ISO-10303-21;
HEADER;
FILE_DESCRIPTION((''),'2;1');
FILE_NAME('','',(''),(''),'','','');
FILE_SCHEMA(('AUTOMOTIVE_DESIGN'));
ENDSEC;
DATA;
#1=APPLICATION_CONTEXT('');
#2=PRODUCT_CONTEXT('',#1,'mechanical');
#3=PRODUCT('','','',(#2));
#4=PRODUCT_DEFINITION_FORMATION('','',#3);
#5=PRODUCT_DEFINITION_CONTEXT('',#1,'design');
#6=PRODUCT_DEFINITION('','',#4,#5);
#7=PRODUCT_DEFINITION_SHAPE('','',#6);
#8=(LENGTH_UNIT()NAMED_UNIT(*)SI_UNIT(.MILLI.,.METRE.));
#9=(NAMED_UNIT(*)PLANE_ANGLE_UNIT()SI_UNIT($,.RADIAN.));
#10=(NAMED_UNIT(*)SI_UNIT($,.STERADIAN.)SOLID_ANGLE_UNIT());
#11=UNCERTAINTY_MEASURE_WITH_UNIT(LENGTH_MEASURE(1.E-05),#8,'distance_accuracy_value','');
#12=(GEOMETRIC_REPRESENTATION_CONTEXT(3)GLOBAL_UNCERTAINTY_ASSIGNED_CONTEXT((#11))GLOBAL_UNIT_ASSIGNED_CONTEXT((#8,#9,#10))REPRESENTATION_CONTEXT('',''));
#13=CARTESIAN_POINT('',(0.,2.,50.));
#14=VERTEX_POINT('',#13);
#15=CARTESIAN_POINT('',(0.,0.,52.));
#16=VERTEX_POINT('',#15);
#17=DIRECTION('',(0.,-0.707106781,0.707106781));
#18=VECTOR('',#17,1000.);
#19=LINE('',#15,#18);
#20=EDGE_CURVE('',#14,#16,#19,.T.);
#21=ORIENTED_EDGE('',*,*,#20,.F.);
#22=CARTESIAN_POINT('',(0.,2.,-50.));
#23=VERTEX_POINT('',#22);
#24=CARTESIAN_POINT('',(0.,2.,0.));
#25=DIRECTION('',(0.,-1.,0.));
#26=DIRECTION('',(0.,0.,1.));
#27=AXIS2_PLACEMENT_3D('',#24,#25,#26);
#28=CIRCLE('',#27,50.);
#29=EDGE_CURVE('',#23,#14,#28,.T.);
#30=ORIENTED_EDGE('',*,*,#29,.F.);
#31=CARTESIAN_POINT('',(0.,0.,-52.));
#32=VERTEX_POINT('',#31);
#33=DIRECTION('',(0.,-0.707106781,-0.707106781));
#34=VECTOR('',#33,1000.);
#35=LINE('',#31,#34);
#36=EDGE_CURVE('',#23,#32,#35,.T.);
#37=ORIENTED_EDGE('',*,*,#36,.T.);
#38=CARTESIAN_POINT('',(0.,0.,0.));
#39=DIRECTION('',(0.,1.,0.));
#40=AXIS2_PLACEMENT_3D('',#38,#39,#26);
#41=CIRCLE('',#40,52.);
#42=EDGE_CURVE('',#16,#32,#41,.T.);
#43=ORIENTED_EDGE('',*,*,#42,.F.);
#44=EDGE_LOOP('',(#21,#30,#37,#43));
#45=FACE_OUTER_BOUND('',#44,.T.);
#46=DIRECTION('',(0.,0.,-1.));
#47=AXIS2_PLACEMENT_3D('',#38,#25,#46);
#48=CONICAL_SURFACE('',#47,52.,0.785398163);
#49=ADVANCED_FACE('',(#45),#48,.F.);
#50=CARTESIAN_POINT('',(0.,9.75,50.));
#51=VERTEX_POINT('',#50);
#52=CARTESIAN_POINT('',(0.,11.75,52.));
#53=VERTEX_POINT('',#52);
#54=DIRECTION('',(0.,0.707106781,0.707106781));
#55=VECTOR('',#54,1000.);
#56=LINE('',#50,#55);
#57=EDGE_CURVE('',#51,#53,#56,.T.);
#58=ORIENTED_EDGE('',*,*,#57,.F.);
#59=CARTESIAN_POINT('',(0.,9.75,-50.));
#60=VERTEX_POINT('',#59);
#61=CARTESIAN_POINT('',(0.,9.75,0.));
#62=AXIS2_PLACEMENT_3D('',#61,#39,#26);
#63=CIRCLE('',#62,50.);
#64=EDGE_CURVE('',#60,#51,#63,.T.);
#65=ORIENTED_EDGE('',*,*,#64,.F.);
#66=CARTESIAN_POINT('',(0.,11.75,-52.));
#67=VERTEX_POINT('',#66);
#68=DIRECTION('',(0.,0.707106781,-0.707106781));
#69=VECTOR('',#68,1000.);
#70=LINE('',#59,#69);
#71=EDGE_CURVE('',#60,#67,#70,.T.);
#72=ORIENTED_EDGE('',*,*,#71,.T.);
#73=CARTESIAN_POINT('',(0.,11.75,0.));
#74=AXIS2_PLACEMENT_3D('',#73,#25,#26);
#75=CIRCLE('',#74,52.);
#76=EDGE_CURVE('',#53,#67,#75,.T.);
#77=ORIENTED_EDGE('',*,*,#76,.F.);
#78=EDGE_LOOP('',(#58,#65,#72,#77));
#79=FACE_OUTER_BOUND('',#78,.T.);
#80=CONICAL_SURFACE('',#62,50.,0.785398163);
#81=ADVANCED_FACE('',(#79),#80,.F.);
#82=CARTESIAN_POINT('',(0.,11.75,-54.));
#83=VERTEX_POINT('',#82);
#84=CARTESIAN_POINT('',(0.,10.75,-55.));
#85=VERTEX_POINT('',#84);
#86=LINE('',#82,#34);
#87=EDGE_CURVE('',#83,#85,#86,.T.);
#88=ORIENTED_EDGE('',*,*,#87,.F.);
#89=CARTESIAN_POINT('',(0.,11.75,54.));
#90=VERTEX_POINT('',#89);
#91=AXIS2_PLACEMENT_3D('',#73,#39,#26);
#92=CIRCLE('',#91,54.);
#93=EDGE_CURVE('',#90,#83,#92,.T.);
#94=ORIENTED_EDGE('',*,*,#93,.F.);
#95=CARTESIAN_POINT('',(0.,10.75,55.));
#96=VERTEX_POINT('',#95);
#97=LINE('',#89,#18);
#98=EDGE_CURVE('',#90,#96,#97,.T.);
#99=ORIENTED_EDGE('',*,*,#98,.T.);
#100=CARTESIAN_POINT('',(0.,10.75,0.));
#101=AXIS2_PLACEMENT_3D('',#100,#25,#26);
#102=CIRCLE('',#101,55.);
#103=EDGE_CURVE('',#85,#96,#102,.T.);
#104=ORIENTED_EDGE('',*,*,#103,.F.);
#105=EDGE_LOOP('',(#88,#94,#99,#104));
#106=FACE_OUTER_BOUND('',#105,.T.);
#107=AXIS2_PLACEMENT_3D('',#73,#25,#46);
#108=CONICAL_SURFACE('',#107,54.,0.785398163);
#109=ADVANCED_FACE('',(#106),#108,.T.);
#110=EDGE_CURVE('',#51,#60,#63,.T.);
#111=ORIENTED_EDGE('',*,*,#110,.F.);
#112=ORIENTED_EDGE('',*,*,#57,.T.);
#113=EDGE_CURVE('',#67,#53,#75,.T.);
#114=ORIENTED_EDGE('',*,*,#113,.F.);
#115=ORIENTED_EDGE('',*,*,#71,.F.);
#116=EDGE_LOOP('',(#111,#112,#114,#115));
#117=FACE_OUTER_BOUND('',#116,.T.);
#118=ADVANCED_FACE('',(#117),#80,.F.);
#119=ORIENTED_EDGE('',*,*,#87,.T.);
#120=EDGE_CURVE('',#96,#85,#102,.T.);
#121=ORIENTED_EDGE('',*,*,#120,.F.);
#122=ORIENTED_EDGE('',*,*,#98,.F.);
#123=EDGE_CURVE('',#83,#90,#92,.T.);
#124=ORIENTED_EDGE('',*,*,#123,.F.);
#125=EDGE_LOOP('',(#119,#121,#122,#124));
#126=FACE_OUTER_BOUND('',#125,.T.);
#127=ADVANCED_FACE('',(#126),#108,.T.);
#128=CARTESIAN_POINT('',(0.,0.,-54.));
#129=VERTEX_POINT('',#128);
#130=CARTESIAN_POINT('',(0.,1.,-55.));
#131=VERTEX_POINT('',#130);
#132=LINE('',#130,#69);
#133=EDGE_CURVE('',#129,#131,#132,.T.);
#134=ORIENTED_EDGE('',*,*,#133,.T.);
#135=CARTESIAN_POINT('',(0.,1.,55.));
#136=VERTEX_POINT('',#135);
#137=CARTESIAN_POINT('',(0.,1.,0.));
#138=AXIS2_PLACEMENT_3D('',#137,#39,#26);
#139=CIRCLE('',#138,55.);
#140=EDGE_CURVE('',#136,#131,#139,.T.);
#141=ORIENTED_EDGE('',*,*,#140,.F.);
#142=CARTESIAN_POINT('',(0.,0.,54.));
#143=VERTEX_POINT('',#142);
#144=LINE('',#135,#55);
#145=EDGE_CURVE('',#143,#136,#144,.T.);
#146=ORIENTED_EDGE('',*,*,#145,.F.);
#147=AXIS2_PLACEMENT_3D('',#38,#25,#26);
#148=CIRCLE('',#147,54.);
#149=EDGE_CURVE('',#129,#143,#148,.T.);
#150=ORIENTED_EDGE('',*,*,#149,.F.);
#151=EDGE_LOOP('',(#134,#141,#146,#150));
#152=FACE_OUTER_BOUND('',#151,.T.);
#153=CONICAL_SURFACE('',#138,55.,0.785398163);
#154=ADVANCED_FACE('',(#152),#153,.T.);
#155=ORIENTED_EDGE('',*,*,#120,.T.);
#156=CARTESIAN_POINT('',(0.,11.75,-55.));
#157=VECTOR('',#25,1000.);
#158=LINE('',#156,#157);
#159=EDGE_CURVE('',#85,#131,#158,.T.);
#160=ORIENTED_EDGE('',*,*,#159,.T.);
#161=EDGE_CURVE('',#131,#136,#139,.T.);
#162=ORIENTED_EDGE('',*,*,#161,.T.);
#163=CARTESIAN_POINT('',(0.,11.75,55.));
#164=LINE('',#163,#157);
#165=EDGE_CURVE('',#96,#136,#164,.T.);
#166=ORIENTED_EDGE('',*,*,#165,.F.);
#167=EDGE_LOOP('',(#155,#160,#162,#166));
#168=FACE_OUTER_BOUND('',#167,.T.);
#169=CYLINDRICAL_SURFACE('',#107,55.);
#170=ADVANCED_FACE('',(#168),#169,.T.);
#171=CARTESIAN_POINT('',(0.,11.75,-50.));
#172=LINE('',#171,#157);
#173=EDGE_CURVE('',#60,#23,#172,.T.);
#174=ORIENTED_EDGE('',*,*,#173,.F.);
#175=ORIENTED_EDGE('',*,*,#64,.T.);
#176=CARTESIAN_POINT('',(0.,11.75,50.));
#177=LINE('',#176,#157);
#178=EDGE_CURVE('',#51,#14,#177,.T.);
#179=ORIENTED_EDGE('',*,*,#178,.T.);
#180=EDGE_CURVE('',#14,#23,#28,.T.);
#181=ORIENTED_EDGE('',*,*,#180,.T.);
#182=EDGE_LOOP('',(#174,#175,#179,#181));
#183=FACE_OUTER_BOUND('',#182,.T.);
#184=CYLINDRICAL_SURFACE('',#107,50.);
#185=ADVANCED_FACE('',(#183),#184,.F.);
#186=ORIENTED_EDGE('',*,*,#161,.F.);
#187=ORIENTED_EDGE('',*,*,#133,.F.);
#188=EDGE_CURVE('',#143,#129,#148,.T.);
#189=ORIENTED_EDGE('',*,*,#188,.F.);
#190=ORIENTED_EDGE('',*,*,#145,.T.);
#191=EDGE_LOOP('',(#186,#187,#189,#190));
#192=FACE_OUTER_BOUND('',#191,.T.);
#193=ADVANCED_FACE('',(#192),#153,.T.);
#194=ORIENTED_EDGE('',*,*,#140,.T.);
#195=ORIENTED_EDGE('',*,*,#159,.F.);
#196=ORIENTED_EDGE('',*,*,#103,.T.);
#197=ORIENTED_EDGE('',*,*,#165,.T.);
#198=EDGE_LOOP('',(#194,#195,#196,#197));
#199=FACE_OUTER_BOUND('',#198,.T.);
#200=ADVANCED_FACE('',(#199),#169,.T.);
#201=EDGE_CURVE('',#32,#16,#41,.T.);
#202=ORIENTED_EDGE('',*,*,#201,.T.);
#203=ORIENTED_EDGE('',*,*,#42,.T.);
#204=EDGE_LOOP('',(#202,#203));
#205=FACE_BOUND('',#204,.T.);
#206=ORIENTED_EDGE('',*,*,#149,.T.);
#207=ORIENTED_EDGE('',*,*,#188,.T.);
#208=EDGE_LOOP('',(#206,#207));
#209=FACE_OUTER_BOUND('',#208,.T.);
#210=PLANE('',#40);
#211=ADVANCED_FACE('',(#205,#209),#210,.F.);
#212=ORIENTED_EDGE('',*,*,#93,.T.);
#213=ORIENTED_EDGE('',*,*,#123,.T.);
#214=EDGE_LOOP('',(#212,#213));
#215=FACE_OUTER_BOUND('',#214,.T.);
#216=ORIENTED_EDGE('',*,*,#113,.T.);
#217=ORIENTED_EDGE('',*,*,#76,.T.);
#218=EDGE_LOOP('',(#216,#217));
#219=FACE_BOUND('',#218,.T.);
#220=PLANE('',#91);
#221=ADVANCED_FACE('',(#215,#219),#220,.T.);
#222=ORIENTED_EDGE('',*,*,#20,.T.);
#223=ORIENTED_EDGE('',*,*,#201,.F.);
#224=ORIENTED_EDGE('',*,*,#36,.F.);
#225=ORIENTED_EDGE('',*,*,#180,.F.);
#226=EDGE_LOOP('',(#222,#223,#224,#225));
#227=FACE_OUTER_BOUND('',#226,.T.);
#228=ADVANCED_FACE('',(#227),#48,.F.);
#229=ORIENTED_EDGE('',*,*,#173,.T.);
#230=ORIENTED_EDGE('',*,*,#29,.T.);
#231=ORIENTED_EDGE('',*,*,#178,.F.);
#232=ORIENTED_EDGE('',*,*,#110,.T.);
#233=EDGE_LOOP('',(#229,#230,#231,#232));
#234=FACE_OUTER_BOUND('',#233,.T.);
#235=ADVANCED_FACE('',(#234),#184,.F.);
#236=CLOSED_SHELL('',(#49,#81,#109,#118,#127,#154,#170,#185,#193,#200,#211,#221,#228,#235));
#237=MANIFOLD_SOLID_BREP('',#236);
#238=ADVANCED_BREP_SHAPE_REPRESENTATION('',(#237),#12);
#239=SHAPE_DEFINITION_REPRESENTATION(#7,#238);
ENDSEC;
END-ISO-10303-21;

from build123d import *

# Parameters (mm, degrees)
SKETCH1_R           = 55
SKETCH1_R_2         = 50
BOSS_EXTRUDE1_DEPTH = 11.75
CHAMFER1_SIZE       = 1
CHAMFER2_SIZE       = 2


with BuildPart() as part:
    # Sketch1 → Boss-Extrude1 (new body)
    with BuildSketch(Plane(origin=(0, 0, 0), x_dir=(1, 0, 0), z_dir=(0, 1, 0))):
        with Locations(Location((0, 0, 0), (0, 0, 270))):
            Circle(SKETCH1_R)
        with Locations(Location((0, 0, 0), (0, 0, 270))):
            Circle(SKETCH1_R_2, mode=Mode.SUBTRACT)
    extrude(amount=BOSS_EXTRUDE1_DEPTH)

    # Chamfer1
    chamfer1_edges = [part.edges().sort_by_distance(p)[0] for p in [
        (0, 0, -55),
        (0, 11.75, -55),
    ]]
    chamfer(chamfer1_edges, length=CHAMFER1_SIZE)

    # Chamfer2
    chamfer2_edges = [part.edges().sort_by_distance(p)[0] for p in [
        (0, 0, -50),
        (0, 11.75, -50),
    ]]
    chamfer(chamfer2_edges, length=CHAMFER2_SIZE)


solid = part.part
